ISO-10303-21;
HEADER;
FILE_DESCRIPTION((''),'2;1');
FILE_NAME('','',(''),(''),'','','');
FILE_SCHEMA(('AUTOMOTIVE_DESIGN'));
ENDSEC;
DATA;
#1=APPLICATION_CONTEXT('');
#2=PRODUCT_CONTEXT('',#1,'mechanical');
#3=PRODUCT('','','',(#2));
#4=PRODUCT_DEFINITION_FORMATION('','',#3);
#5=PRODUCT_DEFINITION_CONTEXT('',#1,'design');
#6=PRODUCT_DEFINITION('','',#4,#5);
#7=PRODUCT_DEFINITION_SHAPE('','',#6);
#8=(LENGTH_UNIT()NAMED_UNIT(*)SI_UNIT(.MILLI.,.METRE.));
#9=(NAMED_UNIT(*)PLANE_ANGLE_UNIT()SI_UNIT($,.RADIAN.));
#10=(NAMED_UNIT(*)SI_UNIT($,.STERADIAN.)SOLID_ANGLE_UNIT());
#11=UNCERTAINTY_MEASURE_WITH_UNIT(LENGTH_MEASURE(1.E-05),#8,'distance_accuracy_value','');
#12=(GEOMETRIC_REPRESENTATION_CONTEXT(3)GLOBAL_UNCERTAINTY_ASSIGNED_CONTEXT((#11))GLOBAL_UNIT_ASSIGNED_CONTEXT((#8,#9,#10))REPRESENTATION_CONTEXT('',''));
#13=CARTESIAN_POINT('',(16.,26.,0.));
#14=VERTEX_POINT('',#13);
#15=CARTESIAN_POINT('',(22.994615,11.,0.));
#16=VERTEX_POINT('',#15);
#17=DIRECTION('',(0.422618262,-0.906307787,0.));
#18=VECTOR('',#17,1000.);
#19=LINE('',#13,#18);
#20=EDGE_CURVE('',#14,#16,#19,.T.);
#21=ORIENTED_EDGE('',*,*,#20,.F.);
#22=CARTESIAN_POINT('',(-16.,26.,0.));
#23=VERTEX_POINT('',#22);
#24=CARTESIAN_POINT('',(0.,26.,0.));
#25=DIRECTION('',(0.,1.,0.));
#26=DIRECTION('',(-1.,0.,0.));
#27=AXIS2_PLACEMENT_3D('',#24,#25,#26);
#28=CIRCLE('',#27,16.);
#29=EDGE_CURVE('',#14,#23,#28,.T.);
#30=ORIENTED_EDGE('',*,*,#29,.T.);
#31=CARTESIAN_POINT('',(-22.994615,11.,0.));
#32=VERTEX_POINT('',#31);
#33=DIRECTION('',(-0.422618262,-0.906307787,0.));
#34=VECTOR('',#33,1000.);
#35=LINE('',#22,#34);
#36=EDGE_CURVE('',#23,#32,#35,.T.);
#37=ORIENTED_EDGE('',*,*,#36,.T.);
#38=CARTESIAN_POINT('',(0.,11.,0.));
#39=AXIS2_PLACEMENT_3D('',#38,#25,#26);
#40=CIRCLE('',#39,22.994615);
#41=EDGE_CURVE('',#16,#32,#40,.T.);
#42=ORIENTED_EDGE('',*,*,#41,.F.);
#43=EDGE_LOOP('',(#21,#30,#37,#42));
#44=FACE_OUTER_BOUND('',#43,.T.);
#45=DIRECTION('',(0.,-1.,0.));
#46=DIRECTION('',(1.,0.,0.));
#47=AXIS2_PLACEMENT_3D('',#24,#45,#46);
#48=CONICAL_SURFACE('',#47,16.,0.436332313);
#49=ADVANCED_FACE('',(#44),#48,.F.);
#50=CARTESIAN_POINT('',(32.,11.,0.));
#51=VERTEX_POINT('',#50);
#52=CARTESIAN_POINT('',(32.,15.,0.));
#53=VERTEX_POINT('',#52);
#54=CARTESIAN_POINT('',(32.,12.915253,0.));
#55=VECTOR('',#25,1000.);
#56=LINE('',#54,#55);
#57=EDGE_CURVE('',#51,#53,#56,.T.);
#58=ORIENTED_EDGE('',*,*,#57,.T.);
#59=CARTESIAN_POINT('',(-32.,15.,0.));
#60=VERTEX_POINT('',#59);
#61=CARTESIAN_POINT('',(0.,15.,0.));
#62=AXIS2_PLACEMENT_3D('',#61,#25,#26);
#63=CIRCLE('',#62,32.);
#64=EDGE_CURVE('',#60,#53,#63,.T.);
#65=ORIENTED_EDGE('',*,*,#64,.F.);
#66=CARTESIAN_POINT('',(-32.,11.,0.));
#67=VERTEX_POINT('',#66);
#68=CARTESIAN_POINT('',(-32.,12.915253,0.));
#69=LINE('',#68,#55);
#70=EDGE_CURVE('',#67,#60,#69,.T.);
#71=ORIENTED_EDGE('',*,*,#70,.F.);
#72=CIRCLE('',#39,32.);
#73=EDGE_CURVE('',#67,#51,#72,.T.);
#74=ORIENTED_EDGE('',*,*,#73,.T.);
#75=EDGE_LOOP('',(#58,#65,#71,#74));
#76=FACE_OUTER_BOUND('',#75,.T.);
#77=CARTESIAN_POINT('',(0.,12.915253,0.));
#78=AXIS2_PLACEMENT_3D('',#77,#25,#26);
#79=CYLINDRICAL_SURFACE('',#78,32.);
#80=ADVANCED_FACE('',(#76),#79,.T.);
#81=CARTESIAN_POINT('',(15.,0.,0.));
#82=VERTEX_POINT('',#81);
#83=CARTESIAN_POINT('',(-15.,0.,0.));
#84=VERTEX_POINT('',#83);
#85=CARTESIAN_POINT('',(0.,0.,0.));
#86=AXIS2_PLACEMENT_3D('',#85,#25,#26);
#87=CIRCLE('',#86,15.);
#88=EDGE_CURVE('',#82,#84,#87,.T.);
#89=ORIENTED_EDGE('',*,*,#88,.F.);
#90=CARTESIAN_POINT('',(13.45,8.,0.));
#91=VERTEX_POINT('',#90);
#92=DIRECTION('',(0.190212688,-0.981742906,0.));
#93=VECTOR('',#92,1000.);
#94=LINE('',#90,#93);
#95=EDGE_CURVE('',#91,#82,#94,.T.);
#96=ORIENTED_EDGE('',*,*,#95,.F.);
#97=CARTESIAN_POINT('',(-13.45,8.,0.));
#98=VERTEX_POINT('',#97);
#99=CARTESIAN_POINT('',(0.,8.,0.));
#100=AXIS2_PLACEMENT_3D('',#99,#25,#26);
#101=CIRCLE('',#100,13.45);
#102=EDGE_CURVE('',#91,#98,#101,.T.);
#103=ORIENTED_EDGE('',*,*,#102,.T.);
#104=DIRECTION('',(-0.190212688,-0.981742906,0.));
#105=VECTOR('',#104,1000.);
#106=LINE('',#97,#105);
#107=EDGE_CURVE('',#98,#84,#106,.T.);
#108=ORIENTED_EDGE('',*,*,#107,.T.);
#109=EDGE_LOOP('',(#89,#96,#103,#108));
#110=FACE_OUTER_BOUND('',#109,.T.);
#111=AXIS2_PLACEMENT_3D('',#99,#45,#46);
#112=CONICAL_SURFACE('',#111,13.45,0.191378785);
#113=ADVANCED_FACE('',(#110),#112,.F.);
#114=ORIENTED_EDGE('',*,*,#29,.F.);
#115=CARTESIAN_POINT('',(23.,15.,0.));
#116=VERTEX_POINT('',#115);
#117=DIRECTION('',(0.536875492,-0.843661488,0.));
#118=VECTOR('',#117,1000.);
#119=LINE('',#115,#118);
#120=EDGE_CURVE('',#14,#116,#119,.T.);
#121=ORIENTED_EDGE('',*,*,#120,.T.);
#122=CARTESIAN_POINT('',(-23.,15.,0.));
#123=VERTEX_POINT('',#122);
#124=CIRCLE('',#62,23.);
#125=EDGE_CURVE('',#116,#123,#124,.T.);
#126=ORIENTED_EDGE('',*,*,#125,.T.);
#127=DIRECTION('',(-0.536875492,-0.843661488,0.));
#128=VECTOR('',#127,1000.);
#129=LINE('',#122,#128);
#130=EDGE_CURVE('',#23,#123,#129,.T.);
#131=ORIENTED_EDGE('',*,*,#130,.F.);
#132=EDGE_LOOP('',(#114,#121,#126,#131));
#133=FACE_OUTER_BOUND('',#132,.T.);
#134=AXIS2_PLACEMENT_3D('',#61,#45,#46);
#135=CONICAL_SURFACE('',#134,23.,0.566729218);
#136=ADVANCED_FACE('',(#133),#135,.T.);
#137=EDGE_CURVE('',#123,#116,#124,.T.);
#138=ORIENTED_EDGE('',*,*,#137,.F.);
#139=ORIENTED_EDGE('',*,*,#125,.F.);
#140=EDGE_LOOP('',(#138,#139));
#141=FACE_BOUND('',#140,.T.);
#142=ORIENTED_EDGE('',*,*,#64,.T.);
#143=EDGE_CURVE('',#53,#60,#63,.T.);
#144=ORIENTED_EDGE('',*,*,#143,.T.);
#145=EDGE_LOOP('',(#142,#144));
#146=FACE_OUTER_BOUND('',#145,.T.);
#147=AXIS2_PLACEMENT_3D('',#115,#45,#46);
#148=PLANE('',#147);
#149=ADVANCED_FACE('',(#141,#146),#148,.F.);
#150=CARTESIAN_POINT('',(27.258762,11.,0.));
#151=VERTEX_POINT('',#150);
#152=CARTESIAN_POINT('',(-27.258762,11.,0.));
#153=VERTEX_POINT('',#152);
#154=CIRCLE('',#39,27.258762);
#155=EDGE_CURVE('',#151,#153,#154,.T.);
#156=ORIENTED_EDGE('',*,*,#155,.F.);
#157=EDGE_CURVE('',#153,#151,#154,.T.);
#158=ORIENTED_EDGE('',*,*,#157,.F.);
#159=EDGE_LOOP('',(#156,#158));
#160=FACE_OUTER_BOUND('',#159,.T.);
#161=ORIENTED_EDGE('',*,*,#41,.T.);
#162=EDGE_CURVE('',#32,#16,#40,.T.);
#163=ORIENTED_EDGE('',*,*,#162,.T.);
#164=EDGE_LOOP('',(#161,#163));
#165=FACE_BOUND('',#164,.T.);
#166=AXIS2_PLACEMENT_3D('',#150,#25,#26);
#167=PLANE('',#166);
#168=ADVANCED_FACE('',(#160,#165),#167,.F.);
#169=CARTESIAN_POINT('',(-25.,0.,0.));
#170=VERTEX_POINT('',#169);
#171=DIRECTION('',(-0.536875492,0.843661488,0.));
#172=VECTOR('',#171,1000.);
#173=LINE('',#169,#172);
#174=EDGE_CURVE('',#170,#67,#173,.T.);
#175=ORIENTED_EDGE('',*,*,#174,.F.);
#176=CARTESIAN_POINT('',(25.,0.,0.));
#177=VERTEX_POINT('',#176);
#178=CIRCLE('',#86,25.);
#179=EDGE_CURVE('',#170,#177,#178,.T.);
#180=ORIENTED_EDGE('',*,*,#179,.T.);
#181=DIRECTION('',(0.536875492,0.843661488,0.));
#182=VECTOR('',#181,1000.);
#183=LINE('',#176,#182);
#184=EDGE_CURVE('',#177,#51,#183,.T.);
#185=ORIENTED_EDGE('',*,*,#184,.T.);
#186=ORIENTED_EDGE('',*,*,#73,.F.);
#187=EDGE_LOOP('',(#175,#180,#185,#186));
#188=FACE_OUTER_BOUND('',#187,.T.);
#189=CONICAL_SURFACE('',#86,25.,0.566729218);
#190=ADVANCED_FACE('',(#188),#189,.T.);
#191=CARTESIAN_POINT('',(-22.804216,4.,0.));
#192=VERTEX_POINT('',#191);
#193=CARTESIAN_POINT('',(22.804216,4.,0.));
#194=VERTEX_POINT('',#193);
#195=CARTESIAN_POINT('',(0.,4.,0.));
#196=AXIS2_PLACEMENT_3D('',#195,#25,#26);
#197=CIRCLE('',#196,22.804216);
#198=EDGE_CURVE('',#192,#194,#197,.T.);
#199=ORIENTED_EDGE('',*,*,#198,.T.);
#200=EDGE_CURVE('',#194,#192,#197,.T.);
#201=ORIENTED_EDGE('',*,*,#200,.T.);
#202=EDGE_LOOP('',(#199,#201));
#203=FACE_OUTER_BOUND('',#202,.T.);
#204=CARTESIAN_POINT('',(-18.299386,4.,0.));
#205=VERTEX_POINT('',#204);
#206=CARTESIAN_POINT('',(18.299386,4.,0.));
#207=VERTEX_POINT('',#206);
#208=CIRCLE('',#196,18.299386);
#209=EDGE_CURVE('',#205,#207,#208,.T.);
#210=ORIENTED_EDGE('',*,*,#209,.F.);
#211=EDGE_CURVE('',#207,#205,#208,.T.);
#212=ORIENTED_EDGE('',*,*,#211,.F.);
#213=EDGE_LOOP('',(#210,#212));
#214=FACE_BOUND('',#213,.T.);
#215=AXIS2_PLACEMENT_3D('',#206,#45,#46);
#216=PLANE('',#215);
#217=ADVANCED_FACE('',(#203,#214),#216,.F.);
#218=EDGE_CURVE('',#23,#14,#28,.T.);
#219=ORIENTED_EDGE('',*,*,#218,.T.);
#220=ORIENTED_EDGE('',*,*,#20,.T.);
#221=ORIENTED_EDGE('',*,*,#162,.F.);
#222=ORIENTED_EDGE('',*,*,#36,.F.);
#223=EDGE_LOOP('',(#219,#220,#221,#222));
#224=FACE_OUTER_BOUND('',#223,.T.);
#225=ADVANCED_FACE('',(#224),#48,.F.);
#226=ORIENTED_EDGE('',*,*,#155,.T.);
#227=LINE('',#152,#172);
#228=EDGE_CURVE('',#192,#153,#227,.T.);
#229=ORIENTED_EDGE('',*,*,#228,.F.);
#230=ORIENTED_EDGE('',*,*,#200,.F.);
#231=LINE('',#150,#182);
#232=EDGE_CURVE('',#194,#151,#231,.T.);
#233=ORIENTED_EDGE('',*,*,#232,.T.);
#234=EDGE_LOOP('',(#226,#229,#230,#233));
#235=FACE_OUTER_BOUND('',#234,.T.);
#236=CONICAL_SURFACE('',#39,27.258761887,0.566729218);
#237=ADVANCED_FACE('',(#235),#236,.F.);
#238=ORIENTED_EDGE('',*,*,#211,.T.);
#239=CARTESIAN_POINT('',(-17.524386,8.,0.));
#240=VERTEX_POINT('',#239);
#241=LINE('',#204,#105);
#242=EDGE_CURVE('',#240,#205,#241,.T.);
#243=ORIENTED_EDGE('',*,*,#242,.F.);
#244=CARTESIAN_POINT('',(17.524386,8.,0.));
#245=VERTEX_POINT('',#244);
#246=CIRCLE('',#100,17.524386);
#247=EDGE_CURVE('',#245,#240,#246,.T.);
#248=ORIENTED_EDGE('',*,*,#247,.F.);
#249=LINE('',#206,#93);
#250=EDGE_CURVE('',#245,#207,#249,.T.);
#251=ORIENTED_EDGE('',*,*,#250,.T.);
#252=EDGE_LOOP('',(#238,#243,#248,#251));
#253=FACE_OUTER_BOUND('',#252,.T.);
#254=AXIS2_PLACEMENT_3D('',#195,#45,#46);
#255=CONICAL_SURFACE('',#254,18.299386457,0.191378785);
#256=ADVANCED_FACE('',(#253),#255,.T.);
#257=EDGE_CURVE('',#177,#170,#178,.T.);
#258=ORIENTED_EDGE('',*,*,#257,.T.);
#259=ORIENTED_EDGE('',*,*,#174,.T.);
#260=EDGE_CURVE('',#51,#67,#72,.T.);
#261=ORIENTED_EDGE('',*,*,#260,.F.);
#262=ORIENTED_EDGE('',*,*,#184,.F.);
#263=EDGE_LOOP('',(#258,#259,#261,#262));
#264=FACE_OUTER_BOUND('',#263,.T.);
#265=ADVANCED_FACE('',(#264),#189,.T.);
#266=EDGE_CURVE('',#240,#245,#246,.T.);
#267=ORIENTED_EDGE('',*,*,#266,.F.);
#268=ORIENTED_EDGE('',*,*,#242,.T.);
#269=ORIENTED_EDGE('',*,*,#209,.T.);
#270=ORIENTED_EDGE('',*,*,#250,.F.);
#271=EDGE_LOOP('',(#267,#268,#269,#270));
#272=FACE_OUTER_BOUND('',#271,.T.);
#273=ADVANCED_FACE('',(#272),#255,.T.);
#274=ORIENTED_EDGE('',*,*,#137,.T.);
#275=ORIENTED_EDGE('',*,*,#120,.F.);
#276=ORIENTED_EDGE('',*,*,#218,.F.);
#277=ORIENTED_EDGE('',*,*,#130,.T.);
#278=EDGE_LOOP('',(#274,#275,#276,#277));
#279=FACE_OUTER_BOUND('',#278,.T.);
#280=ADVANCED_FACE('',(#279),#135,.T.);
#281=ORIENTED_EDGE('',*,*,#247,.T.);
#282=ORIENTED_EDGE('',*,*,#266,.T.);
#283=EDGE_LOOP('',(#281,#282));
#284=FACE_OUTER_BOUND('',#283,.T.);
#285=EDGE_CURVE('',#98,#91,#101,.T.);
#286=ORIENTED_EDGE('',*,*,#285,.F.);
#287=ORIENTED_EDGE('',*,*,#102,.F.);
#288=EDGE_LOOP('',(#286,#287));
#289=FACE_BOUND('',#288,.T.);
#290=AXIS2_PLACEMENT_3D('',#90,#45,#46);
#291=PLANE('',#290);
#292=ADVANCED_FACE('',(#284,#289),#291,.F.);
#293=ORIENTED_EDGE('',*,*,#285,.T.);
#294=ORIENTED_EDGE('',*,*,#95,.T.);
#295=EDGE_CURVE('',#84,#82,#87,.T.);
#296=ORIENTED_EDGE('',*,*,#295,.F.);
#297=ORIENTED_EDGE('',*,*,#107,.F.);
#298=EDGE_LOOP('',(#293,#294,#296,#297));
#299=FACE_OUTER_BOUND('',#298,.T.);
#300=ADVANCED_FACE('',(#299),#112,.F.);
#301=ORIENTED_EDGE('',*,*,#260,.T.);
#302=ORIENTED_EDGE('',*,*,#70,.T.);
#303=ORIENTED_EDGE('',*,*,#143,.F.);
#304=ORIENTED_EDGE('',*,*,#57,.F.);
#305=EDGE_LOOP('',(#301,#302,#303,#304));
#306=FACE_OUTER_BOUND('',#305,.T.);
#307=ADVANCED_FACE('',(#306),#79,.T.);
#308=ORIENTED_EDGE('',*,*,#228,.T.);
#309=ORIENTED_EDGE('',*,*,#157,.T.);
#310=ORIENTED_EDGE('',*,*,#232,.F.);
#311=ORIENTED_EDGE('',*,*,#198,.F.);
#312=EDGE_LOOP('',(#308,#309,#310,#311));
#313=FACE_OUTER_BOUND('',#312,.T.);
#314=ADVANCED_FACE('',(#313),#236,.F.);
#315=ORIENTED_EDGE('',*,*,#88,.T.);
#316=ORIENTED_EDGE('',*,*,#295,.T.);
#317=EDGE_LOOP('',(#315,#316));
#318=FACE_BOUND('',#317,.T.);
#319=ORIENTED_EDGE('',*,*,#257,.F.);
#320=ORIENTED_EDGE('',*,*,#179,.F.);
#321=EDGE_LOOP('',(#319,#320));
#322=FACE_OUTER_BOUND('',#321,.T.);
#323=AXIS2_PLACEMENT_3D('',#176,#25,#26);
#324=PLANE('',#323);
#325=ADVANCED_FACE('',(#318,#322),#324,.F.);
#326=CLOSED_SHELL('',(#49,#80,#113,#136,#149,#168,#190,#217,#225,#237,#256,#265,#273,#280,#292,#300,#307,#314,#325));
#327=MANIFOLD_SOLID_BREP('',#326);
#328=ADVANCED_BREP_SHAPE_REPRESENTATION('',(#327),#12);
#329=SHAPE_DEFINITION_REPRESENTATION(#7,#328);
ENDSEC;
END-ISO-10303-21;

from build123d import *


with BuildPart() as part:
    # 草图1 → 旋转1 (revolve)
    with BuildSketch(Plane.XY, mode=Mode.PRIVATE) as revolve_1_sk:
        Polygon((16, 26), (23, 15), (32, 15), (32, 11), (25, 0), (15, 0), (13.45, 8), (17.524386457, 8), (18.299386457, 4), (22.804216433, 4), (27.258761887, 11), (22.994614872, 11), align=None)
    revolve(revolve_1_sk.sketch.rotate(Axis((0, 12.915252942, 0), (0, -1, 0)), 180), axis=Axis((0, 12.915252942, 0), (0, -1, 0)))


solid = part.part
